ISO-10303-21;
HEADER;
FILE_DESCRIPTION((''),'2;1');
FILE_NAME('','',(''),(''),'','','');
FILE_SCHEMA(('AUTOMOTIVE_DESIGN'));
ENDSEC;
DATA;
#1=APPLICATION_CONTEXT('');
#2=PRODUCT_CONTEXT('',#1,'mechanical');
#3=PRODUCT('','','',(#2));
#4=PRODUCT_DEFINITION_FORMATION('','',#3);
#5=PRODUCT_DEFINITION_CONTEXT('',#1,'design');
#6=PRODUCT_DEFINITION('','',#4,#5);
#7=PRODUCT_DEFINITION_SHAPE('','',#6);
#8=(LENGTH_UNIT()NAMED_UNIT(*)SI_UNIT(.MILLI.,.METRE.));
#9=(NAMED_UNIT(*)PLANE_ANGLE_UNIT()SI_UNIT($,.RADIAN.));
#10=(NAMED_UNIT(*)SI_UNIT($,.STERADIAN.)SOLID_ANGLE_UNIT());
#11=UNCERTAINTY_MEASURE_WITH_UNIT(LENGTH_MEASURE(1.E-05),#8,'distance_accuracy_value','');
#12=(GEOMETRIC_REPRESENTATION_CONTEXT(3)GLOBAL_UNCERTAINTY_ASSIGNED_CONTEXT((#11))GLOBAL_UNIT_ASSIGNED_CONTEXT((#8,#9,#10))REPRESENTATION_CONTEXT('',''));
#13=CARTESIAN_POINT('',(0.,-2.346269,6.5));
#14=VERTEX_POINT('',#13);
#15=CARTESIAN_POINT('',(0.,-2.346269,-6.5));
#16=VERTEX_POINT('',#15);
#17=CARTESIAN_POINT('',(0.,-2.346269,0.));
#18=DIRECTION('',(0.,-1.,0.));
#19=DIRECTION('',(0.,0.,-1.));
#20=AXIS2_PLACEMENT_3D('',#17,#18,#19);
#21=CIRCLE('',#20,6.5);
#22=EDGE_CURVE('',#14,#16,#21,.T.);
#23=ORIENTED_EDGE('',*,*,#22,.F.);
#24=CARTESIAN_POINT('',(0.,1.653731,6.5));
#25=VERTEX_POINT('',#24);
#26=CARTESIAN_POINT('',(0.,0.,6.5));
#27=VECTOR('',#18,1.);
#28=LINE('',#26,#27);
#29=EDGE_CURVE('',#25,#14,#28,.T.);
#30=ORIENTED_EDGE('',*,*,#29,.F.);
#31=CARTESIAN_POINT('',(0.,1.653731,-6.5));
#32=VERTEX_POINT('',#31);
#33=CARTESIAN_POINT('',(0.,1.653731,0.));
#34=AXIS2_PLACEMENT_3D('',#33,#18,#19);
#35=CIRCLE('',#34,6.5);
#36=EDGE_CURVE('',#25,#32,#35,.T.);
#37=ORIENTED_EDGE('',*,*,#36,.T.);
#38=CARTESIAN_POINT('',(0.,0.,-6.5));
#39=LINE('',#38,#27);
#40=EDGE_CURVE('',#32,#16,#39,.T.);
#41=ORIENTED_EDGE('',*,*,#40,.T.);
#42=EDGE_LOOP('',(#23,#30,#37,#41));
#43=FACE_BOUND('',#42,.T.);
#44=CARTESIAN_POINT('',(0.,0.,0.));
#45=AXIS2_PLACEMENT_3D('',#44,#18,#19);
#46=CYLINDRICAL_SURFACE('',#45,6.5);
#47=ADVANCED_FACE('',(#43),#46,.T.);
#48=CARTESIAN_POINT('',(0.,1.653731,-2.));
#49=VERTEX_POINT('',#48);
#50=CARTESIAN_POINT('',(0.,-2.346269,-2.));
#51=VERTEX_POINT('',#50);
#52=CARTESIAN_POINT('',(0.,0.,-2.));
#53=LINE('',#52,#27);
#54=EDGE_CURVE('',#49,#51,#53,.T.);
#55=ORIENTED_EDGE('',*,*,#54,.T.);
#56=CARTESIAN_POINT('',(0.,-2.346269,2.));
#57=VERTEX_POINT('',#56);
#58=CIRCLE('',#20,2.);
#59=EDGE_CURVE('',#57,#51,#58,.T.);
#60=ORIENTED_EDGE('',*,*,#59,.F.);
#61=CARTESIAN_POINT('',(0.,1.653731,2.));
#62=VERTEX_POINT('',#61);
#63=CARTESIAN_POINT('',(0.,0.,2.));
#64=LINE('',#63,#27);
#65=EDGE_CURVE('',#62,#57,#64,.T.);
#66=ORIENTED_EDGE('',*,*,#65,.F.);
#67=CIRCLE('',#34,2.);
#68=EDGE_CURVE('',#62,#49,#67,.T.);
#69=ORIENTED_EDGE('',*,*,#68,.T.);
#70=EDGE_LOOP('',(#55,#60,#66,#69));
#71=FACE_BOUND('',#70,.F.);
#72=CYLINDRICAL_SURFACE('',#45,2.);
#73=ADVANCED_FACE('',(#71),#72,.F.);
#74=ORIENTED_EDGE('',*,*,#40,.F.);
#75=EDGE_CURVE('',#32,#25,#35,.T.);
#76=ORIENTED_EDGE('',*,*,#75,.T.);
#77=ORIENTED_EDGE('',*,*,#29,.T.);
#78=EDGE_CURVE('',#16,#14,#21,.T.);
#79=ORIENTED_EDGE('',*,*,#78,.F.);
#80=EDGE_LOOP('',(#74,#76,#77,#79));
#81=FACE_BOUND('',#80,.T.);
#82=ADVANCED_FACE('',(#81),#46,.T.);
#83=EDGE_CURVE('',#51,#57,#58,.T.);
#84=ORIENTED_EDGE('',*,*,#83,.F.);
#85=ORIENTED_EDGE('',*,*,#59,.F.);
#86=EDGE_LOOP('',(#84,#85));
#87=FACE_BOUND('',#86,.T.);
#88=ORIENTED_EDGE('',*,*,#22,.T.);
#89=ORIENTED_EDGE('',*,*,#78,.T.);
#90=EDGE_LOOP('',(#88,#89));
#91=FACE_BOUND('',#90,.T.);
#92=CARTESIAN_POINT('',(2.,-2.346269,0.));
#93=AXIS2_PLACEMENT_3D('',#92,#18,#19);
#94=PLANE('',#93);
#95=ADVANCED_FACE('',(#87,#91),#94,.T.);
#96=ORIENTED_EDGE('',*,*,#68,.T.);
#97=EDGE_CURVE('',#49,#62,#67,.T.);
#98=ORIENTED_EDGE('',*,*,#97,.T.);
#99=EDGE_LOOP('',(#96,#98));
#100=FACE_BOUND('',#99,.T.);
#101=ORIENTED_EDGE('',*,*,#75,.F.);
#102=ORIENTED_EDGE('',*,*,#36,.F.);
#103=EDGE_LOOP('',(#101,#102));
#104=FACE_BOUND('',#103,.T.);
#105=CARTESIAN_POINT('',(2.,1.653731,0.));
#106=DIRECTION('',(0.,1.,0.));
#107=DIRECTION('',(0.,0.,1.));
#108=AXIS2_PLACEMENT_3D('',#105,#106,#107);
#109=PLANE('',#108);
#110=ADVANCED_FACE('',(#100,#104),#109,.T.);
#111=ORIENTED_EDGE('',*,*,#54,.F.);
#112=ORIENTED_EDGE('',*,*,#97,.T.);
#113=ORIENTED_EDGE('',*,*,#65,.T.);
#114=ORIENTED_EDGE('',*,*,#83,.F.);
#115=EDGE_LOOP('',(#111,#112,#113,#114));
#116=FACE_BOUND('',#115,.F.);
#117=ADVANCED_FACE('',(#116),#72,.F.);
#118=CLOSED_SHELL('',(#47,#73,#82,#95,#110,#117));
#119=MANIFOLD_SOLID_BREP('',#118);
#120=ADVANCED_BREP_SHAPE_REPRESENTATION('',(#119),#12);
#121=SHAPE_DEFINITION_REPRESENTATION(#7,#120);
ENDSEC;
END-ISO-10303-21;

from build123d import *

# Parameters (mm, degrees)
SKETCH_1_W = 4.5
SKETCH_1_H = 4


with BuildPart() as part:
    # 草图1 → 旋转1 (revolve)
    with BuildSketch(Plane.XY, mode=Mode.PRIVATE) as revolve_1_sk:
        with Locations((4.25, -0.346268657)):
            Rectangle(SKETCH_1_W, SKETCH_1_H)
    revolve(revolve_1_sk.sketch.rotate(Axis((0, 0, 0), (0, 1, 0)), 90), axis=Axis((0, 0, 0), (0, 1, 0)))


solid = part.part
